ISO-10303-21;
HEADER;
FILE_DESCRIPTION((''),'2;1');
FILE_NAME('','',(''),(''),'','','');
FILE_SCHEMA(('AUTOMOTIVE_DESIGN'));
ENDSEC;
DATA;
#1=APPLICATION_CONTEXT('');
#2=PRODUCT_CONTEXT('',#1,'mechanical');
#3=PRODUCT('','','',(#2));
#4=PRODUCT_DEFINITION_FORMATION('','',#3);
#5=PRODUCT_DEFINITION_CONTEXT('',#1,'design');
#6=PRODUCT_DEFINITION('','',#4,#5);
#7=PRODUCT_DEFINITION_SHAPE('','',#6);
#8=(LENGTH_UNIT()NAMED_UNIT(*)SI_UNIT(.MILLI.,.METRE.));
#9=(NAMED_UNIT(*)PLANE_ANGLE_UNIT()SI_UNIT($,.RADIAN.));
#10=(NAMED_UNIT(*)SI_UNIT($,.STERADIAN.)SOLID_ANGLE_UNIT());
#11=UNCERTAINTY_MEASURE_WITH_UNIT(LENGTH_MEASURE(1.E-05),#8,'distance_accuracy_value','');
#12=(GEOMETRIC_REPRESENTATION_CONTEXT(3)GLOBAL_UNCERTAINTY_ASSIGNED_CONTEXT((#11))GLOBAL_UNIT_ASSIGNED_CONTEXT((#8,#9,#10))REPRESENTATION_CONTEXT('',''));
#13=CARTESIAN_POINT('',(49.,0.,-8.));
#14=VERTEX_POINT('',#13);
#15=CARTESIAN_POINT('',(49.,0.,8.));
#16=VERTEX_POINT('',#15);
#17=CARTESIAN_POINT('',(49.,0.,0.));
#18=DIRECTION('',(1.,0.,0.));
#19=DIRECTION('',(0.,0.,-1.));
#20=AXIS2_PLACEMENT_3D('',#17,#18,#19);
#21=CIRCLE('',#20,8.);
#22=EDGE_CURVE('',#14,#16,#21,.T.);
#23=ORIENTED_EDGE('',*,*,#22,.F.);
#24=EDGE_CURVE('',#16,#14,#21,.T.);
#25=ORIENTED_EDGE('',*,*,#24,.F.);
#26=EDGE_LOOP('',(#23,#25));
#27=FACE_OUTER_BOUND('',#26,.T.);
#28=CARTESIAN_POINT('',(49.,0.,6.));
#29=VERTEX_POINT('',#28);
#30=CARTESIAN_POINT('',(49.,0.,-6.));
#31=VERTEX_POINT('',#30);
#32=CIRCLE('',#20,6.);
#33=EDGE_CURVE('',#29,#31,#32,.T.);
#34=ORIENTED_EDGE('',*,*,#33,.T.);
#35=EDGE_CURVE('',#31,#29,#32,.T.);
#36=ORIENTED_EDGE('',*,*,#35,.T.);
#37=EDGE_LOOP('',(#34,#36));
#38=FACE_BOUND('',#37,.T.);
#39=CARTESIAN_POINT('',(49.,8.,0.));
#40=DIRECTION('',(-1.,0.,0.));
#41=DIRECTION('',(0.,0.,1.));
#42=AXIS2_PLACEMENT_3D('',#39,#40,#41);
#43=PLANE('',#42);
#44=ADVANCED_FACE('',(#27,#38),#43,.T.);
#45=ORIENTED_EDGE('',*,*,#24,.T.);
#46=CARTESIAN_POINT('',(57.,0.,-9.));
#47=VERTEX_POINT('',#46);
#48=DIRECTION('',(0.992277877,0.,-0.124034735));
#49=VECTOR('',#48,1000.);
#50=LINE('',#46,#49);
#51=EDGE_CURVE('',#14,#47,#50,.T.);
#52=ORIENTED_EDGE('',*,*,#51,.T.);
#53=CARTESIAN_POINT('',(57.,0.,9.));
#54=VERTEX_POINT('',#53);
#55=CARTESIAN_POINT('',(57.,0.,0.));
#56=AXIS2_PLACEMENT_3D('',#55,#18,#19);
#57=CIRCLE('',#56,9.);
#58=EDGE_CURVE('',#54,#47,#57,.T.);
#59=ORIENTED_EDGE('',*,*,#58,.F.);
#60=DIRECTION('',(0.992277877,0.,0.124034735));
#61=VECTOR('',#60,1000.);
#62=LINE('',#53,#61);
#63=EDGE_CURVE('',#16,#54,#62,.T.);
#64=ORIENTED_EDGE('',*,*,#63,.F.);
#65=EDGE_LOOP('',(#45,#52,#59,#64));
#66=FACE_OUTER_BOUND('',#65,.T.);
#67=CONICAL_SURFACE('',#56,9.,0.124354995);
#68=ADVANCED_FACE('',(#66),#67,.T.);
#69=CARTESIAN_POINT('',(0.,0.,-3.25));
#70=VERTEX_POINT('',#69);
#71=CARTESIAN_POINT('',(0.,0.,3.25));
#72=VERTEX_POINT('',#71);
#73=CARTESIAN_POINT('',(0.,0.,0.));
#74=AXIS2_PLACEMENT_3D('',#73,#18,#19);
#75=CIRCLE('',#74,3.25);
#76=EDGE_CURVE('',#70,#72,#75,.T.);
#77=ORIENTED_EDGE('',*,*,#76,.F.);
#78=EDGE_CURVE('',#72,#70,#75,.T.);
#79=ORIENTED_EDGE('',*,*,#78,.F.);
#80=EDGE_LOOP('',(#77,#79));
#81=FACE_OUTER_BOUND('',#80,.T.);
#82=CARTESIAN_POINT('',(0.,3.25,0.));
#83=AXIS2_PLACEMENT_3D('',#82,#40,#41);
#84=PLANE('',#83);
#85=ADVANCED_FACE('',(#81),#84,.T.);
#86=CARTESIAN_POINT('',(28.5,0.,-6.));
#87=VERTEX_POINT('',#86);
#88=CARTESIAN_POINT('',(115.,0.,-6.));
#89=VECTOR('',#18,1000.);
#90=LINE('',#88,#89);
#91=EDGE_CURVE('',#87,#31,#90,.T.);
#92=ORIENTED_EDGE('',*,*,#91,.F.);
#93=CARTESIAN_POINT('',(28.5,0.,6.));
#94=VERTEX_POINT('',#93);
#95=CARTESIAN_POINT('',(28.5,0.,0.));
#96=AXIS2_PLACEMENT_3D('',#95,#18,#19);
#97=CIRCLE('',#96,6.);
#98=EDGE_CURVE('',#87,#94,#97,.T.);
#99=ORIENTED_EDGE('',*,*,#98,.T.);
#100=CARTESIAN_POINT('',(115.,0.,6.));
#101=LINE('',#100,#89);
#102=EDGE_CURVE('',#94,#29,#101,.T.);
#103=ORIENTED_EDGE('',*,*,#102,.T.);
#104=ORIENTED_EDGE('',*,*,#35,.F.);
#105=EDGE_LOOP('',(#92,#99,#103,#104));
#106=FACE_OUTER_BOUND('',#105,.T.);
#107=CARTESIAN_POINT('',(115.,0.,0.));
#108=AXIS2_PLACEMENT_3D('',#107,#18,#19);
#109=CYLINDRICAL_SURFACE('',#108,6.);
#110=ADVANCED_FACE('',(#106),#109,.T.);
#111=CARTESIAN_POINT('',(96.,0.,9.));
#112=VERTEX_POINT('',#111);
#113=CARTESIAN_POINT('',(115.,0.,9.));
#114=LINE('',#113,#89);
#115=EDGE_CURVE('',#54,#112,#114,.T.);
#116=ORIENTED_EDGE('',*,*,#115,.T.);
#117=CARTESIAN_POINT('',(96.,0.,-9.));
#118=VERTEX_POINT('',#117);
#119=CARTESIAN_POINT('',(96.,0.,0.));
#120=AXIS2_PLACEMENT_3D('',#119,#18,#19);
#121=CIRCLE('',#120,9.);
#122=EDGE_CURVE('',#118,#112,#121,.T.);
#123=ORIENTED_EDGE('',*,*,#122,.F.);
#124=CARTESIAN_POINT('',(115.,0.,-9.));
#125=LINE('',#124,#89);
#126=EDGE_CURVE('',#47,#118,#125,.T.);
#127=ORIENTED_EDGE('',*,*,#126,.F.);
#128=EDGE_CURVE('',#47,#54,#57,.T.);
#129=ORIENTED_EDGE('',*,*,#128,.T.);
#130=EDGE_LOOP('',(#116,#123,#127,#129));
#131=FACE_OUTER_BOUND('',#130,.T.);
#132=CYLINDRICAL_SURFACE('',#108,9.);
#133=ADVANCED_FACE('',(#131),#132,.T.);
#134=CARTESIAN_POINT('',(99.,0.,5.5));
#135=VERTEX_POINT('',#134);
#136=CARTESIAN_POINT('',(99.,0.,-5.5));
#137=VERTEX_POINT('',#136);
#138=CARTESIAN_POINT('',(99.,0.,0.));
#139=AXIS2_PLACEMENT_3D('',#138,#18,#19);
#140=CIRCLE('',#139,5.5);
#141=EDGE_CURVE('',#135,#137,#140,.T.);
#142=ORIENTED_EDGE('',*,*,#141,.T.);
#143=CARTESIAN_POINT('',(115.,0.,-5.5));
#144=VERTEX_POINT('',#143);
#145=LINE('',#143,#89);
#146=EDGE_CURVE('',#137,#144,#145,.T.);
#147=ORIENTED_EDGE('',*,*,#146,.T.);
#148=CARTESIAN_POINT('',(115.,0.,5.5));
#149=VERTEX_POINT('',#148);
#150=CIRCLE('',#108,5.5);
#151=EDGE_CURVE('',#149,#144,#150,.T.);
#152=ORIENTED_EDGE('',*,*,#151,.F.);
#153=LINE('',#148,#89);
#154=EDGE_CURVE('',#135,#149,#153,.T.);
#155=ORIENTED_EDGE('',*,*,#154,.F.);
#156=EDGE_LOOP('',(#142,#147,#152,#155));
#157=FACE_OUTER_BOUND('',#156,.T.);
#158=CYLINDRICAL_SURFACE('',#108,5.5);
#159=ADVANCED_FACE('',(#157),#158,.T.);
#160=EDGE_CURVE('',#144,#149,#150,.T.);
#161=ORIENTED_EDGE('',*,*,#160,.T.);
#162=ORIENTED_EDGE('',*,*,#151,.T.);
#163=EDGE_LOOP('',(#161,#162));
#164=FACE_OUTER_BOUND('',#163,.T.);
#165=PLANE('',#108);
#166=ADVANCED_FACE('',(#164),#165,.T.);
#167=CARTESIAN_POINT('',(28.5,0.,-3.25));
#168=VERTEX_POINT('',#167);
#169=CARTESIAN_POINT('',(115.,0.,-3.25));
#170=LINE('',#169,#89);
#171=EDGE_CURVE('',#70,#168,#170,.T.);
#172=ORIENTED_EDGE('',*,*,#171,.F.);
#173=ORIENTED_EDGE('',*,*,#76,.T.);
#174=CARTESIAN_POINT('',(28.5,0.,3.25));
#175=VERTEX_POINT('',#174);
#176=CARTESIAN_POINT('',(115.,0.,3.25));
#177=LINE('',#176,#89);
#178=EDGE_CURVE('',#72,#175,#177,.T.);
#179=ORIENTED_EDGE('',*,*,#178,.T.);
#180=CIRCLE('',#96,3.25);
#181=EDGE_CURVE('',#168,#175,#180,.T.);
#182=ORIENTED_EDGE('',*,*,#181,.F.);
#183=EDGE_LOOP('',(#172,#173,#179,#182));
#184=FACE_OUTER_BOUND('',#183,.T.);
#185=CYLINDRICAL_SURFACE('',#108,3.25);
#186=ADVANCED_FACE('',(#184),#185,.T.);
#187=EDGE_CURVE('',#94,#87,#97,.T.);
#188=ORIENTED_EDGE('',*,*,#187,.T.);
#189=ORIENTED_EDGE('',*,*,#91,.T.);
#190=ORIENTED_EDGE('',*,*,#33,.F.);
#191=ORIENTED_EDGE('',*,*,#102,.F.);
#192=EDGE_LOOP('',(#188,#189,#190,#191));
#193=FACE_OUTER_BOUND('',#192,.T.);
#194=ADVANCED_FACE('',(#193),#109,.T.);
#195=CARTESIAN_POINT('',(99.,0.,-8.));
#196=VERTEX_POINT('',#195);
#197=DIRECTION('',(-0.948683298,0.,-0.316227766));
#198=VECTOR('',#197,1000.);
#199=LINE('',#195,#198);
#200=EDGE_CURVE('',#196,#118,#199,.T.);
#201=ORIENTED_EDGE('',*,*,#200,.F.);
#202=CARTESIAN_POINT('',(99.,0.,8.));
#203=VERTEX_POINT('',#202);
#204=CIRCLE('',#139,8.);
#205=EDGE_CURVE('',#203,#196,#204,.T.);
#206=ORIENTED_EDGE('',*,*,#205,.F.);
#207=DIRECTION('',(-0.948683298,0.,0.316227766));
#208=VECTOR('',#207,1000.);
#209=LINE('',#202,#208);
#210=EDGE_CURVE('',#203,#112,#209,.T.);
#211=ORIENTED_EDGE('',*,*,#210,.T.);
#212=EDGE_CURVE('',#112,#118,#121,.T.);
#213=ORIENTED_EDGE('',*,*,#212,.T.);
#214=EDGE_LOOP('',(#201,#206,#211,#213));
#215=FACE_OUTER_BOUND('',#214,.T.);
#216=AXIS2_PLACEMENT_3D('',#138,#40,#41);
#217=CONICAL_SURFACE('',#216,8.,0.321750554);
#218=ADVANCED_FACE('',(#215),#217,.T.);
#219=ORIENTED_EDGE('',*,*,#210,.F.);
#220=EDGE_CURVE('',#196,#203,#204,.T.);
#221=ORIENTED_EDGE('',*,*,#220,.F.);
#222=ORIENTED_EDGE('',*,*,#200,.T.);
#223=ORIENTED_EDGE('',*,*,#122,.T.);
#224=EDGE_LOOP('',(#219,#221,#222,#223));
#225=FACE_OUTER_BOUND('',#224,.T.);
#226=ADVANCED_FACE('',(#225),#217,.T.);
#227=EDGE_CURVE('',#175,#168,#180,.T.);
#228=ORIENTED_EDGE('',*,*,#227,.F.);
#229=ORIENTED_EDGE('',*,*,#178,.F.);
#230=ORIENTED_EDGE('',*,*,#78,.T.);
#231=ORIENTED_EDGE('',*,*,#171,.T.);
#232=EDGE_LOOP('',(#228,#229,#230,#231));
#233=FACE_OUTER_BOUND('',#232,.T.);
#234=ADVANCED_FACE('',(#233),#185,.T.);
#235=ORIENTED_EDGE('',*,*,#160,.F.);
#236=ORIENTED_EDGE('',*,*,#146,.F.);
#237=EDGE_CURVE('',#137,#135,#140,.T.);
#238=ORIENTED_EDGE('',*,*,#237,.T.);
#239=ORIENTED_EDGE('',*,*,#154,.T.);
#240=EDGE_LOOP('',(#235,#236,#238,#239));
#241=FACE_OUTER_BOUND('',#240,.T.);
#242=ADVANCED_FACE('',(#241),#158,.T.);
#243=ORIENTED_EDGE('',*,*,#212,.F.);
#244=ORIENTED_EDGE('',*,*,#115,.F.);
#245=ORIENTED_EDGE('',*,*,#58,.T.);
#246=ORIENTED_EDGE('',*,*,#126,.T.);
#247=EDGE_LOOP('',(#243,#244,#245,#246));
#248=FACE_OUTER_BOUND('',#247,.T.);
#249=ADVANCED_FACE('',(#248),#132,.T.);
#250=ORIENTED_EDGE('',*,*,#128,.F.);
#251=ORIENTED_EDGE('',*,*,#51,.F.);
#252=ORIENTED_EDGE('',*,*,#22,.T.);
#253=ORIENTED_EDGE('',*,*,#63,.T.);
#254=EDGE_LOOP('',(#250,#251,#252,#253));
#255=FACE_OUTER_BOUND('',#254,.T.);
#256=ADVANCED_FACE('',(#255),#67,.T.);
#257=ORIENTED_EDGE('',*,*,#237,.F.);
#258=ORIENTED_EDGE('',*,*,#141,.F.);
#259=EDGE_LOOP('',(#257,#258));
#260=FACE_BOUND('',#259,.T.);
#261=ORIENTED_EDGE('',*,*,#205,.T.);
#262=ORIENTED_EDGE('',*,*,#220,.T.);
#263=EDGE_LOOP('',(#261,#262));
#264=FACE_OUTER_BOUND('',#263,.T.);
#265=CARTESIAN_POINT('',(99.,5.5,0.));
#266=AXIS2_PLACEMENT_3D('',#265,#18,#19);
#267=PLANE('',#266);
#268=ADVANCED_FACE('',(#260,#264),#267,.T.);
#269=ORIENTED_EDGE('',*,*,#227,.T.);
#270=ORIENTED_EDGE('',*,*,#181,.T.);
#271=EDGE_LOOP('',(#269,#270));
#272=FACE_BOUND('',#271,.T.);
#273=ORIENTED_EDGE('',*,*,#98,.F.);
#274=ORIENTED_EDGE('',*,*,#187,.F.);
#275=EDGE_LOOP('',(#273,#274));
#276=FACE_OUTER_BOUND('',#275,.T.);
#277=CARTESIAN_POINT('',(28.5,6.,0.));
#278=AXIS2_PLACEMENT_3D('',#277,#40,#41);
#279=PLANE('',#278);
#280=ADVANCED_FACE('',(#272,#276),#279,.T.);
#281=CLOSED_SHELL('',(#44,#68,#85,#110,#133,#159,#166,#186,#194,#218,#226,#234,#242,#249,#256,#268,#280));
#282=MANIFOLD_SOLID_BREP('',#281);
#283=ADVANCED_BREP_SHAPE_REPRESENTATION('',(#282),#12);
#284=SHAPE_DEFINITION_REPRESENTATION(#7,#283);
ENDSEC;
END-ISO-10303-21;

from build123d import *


with BuildPart() as part:
    # Sketch1 → Revolve1 (revolve)
    with BuildSketch(Plane.XY, mode=Mode.PRIVATE) as revolve1_sk:
        Polygon((28.5, 3.25), (0, 3.25), (0, 0), (115, 0), (115, 5.5), (99, 5.5), (99, 8), (96, 9), (57, 9), (49, 8), (49, 6), (28.5, 6), align=None)
    revolve(revolve1_sk.sketch.rotate(Axis((115, 0, 0), (-1, 0, 0)), 90), axis=Axis((115, 0, 0), (-1, 0, 0)))


solid = part.part
